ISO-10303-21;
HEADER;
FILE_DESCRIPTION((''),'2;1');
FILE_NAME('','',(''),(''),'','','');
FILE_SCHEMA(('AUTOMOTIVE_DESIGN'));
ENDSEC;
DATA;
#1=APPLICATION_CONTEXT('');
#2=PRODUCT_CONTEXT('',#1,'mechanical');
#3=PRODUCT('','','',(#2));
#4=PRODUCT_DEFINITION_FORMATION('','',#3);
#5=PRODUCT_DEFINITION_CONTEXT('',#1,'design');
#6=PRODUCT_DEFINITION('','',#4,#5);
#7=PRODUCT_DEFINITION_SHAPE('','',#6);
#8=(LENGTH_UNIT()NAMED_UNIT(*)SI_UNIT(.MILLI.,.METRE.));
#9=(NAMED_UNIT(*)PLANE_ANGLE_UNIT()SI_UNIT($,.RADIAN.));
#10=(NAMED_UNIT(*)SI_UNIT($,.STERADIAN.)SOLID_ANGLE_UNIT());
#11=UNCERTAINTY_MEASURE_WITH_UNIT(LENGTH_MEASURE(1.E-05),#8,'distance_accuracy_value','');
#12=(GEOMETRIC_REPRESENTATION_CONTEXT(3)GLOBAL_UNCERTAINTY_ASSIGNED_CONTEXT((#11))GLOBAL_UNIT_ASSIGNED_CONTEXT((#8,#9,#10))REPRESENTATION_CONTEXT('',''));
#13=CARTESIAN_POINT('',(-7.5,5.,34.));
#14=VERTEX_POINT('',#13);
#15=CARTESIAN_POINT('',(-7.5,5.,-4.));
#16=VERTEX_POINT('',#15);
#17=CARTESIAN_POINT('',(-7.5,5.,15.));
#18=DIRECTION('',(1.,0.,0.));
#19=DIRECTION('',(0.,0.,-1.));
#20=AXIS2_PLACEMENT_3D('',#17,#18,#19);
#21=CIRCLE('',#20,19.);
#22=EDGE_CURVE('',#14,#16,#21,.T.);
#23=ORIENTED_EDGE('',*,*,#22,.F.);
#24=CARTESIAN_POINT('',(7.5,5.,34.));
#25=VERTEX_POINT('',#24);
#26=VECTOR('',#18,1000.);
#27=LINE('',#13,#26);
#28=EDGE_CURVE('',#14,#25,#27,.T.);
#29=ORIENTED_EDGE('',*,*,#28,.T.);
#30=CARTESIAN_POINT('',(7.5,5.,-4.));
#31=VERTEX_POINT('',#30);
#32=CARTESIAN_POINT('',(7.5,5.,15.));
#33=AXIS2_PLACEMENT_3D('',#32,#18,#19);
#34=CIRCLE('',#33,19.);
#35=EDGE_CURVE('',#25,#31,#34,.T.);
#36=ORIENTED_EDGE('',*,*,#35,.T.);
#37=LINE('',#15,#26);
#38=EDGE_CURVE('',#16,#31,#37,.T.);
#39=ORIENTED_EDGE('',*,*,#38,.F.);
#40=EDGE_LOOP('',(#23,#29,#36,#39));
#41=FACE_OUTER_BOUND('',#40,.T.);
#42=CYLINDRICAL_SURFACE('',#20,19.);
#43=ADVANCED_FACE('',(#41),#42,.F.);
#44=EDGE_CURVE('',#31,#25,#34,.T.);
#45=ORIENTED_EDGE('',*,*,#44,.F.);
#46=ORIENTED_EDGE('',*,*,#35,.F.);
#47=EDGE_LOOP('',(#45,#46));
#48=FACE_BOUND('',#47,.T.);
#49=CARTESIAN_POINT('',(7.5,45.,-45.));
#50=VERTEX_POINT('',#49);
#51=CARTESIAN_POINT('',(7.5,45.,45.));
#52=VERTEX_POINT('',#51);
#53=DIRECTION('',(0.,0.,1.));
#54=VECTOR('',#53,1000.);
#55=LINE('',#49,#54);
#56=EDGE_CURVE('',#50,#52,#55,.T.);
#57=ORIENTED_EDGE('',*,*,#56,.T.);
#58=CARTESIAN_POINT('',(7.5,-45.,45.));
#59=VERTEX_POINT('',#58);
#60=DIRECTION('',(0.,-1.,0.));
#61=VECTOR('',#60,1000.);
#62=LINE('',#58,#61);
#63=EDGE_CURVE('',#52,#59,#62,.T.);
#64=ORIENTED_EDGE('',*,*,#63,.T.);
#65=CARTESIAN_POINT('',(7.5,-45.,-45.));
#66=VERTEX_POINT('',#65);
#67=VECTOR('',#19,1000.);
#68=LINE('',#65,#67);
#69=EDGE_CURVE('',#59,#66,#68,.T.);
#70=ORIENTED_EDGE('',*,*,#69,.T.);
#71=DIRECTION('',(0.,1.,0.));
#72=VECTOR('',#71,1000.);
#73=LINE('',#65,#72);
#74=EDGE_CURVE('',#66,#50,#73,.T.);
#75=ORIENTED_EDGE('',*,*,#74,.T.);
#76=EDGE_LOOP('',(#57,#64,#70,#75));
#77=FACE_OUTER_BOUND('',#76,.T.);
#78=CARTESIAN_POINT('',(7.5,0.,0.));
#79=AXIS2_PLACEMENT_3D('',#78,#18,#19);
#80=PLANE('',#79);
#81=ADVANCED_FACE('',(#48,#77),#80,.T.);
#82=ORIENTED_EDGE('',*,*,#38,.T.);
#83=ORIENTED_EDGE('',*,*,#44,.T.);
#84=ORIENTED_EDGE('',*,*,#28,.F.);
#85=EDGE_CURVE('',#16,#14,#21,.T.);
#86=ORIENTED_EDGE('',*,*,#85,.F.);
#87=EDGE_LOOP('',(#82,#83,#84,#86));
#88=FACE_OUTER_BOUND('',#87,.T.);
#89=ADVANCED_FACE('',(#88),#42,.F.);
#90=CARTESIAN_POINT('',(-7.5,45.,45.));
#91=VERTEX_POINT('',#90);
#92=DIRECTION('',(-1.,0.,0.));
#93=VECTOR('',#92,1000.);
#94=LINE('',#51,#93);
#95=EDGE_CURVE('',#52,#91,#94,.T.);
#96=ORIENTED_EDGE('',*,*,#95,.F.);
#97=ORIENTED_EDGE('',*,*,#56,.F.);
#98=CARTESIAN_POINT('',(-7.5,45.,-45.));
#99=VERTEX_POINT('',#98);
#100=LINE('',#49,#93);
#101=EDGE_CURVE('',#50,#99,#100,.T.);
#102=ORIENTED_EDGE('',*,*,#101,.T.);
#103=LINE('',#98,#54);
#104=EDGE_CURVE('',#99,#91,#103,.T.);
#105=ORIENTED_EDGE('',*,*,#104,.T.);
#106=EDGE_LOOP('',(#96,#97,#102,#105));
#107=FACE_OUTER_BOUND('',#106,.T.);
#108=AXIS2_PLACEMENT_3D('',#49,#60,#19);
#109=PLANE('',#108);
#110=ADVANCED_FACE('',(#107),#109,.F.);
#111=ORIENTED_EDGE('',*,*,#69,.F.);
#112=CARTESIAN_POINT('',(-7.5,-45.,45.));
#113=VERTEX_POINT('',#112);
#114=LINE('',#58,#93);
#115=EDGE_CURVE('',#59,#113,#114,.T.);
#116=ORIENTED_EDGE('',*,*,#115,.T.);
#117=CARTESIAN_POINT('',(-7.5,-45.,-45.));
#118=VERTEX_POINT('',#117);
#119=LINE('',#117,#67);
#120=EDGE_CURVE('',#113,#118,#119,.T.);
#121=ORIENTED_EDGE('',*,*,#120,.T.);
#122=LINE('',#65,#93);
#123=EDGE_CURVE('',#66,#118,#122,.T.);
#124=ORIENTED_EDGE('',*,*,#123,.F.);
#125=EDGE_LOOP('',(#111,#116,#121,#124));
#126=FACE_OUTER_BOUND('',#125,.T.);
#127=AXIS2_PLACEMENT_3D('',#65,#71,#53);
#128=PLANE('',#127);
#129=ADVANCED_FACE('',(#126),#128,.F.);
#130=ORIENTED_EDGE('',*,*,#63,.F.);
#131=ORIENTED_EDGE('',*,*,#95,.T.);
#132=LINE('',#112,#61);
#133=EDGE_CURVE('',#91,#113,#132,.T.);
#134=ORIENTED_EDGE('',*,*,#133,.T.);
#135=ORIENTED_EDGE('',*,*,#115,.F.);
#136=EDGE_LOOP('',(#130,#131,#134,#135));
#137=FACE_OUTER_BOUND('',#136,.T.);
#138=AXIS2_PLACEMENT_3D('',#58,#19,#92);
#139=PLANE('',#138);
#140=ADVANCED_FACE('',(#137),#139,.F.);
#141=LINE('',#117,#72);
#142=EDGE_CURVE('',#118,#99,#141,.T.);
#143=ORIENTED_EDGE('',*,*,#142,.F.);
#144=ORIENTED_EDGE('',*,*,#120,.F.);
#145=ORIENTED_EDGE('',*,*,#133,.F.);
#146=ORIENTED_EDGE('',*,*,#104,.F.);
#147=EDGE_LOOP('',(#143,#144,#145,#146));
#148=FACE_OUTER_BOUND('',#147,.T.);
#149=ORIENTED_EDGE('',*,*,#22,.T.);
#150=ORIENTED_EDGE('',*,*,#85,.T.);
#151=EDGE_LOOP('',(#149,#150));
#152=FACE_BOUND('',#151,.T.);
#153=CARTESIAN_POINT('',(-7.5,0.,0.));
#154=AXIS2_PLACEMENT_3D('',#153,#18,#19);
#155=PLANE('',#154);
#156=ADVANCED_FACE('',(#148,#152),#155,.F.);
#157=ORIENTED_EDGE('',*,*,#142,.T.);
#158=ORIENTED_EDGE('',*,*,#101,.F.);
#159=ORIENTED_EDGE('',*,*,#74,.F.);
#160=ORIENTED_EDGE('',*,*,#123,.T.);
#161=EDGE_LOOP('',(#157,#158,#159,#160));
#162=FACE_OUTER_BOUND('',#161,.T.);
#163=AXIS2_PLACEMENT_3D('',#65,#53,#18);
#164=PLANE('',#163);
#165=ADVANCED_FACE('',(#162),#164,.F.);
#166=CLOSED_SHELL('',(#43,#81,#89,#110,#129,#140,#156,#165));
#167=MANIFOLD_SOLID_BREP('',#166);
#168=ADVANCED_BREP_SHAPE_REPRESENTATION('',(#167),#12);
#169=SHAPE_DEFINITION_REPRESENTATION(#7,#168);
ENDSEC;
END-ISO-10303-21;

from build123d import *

# Parameters (mm, degrees)
SKETCH1_W           = 90
SKETCH1_H           = 90
BOSS_EXTRUDE1_DEPTH = 7.5
SKETCH2_R           = 19
CUT_EXTRUDE1_DEPTH  = 15


with BuildPart() as part:
    # Sketch1 → Boss-Extrude1 (new, symmetric)
    with BuildSketch(Plane(origin=(0, 0, 0), x_dir=(0, 0, -1), z_dir=(1, 0, 0))):
        Rectangle(SKETCH1_W, SKETCH1_H)
    extrude(amount=BOSS_EXTRUDE1_DEPTH, both=True)

    # Sketch2 → Cut-Extrude1 (cut)
    with BuildSketch(Plane(origin=(7.5, 0, 0), x_dir=(0, 0, -1), z_dir=(1, 0, 0))):
        with Locations((-15, 5)):
            Circle(SKETCH2_R)
    extrude(amount=-CUT_EXTRUDE1_DEPTH, mode=Mode.SUBTRACT)


solid = part.part
